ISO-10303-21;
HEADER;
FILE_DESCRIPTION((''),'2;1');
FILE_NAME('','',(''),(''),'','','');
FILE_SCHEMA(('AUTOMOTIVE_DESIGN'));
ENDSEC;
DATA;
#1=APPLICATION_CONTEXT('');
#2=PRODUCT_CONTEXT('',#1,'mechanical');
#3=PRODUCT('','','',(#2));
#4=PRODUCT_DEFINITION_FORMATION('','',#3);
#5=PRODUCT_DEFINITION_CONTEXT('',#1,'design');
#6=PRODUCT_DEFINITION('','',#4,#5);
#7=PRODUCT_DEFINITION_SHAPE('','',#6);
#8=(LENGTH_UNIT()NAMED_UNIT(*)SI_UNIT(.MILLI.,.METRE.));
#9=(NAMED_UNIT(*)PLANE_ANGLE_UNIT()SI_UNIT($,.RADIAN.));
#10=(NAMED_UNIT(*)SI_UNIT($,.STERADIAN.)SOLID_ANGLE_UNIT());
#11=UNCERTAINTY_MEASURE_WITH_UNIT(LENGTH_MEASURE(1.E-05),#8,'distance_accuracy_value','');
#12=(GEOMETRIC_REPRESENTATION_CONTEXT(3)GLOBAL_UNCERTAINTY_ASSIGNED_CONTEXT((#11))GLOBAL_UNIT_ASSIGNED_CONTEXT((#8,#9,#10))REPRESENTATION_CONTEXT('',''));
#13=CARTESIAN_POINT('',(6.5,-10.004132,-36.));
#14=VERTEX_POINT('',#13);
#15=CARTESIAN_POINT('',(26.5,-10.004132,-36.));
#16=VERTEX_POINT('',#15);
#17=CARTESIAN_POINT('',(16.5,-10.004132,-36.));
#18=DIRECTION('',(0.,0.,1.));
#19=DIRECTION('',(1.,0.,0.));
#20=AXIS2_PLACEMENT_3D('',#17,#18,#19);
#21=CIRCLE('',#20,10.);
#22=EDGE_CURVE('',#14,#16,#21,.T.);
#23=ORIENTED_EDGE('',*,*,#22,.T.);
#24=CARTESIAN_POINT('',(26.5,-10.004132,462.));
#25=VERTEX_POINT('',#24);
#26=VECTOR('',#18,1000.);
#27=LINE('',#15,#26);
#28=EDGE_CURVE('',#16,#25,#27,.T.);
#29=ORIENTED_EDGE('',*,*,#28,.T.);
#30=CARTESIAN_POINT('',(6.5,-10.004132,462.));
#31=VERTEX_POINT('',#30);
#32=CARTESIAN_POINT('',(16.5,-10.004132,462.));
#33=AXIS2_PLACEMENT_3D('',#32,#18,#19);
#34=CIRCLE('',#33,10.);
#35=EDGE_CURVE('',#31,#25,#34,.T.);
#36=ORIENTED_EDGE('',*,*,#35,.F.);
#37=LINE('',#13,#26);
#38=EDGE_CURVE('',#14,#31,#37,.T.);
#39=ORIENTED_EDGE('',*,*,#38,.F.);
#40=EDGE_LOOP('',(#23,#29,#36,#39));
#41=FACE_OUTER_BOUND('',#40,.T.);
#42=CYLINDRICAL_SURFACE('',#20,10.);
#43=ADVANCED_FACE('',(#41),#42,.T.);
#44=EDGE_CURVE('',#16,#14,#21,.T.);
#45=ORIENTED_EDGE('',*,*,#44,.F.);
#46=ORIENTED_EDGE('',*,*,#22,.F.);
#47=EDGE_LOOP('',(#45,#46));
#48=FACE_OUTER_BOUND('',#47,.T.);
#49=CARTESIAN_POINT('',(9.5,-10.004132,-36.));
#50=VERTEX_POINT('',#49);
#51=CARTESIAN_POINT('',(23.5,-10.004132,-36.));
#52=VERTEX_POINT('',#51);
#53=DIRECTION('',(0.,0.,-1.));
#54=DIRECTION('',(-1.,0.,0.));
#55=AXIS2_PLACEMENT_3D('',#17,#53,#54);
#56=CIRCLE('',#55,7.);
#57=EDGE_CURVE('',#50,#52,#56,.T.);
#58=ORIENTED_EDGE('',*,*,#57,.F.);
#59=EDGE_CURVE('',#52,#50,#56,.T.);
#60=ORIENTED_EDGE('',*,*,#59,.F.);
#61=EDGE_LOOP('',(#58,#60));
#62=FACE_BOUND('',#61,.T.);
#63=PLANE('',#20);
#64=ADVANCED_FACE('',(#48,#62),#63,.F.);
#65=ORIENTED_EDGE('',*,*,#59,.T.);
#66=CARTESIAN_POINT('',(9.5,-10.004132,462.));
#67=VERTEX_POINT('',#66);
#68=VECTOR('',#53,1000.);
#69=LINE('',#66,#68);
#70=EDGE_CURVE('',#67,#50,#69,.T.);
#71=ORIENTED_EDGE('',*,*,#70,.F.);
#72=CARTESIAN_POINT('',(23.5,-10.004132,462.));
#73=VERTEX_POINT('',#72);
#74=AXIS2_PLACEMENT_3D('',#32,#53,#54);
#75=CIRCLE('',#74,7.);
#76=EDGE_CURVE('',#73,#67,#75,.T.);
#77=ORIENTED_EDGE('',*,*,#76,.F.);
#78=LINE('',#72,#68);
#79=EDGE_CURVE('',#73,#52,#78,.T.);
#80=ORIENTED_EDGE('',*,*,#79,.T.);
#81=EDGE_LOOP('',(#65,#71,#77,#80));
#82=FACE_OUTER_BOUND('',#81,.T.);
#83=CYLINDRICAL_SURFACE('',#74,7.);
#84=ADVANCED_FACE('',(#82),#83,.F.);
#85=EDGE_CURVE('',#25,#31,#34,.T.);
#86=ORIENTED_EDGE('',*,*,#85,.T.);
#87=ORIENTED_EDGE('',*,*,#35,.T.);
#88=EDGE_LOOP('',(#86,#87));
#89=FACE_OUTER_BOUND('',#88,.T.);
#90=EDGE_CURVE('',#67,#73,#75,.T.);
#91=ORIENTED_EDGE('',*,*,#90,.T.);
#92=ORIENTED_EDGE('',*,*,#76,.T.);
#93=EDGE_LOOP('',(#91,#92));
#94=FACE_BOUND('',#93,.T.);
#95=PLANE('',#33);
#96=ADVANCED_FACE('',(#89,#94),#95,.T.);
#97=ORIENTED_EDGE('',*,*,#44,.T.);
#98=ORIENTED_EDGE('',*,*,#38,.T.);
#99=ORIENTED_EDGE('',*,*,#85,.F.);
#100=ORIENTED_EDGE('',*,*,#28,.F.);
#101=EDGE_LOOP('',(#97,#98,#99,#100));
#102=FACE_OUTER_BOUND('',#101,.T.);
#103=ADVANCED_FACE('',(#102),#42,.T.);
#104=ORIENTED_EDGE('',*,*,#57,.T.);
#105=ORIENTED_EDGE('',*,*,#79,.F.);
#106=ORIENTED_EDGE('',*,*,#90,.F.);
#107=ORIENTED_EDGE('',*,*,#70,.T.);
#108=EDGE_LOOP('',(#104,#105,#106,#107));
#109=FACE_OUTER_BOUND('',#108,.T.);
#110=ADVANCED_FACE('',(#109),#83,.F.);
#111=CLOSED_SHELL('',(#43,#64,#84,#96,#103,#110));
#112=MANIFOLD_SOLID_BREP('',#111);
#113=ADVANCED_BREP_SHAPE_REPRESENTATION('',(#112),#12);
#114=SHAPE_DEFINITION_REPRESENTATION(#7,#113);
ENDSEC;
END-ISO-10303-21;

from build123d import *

# Parameters (mm, degrees)
BOSS_EXTRUDE1_DEPTH      = 462
BOSS_EXTRUDE1_DEPTH_BACK = 36
SKETCH4_R                = 10
SKETCH5_R                = 7
CUT_EXTRUDE1_DEPTH       = 500.105615354


with BuildPart() as part:
    # Sketch4 → Boss-Extrude1 (new, two sides: drawn at the far end of the back side and taken through both)
    with BuildSketch(Plane.XY.offset(-BOSS_EXTRUDE1_DEPTH_BACK)):
        with Locations((16.5, -10.004131531)):
            Circle(SKETCH4_R)
    extrude(amount=BOSS_EXTRUDE1_DEPTH + BOSS_EXTRUDE1_DEPTH_BACK)

    # Sketch5 → Cut-Extrude1 (cut, through all)
    with BuildSketch(Plane(origin=(0, 0, -36), x_dir=(-1, 0, 0), z_dir=(0, 0, -1))):
        with Locations((-16.5, -10.004131531)):
            Circle(SKETCH5_R)
    extrude(amount=-CUT_EXTRUDE1_DEPTH, mode=Mode.SUBTRACT)


solid = part.part
